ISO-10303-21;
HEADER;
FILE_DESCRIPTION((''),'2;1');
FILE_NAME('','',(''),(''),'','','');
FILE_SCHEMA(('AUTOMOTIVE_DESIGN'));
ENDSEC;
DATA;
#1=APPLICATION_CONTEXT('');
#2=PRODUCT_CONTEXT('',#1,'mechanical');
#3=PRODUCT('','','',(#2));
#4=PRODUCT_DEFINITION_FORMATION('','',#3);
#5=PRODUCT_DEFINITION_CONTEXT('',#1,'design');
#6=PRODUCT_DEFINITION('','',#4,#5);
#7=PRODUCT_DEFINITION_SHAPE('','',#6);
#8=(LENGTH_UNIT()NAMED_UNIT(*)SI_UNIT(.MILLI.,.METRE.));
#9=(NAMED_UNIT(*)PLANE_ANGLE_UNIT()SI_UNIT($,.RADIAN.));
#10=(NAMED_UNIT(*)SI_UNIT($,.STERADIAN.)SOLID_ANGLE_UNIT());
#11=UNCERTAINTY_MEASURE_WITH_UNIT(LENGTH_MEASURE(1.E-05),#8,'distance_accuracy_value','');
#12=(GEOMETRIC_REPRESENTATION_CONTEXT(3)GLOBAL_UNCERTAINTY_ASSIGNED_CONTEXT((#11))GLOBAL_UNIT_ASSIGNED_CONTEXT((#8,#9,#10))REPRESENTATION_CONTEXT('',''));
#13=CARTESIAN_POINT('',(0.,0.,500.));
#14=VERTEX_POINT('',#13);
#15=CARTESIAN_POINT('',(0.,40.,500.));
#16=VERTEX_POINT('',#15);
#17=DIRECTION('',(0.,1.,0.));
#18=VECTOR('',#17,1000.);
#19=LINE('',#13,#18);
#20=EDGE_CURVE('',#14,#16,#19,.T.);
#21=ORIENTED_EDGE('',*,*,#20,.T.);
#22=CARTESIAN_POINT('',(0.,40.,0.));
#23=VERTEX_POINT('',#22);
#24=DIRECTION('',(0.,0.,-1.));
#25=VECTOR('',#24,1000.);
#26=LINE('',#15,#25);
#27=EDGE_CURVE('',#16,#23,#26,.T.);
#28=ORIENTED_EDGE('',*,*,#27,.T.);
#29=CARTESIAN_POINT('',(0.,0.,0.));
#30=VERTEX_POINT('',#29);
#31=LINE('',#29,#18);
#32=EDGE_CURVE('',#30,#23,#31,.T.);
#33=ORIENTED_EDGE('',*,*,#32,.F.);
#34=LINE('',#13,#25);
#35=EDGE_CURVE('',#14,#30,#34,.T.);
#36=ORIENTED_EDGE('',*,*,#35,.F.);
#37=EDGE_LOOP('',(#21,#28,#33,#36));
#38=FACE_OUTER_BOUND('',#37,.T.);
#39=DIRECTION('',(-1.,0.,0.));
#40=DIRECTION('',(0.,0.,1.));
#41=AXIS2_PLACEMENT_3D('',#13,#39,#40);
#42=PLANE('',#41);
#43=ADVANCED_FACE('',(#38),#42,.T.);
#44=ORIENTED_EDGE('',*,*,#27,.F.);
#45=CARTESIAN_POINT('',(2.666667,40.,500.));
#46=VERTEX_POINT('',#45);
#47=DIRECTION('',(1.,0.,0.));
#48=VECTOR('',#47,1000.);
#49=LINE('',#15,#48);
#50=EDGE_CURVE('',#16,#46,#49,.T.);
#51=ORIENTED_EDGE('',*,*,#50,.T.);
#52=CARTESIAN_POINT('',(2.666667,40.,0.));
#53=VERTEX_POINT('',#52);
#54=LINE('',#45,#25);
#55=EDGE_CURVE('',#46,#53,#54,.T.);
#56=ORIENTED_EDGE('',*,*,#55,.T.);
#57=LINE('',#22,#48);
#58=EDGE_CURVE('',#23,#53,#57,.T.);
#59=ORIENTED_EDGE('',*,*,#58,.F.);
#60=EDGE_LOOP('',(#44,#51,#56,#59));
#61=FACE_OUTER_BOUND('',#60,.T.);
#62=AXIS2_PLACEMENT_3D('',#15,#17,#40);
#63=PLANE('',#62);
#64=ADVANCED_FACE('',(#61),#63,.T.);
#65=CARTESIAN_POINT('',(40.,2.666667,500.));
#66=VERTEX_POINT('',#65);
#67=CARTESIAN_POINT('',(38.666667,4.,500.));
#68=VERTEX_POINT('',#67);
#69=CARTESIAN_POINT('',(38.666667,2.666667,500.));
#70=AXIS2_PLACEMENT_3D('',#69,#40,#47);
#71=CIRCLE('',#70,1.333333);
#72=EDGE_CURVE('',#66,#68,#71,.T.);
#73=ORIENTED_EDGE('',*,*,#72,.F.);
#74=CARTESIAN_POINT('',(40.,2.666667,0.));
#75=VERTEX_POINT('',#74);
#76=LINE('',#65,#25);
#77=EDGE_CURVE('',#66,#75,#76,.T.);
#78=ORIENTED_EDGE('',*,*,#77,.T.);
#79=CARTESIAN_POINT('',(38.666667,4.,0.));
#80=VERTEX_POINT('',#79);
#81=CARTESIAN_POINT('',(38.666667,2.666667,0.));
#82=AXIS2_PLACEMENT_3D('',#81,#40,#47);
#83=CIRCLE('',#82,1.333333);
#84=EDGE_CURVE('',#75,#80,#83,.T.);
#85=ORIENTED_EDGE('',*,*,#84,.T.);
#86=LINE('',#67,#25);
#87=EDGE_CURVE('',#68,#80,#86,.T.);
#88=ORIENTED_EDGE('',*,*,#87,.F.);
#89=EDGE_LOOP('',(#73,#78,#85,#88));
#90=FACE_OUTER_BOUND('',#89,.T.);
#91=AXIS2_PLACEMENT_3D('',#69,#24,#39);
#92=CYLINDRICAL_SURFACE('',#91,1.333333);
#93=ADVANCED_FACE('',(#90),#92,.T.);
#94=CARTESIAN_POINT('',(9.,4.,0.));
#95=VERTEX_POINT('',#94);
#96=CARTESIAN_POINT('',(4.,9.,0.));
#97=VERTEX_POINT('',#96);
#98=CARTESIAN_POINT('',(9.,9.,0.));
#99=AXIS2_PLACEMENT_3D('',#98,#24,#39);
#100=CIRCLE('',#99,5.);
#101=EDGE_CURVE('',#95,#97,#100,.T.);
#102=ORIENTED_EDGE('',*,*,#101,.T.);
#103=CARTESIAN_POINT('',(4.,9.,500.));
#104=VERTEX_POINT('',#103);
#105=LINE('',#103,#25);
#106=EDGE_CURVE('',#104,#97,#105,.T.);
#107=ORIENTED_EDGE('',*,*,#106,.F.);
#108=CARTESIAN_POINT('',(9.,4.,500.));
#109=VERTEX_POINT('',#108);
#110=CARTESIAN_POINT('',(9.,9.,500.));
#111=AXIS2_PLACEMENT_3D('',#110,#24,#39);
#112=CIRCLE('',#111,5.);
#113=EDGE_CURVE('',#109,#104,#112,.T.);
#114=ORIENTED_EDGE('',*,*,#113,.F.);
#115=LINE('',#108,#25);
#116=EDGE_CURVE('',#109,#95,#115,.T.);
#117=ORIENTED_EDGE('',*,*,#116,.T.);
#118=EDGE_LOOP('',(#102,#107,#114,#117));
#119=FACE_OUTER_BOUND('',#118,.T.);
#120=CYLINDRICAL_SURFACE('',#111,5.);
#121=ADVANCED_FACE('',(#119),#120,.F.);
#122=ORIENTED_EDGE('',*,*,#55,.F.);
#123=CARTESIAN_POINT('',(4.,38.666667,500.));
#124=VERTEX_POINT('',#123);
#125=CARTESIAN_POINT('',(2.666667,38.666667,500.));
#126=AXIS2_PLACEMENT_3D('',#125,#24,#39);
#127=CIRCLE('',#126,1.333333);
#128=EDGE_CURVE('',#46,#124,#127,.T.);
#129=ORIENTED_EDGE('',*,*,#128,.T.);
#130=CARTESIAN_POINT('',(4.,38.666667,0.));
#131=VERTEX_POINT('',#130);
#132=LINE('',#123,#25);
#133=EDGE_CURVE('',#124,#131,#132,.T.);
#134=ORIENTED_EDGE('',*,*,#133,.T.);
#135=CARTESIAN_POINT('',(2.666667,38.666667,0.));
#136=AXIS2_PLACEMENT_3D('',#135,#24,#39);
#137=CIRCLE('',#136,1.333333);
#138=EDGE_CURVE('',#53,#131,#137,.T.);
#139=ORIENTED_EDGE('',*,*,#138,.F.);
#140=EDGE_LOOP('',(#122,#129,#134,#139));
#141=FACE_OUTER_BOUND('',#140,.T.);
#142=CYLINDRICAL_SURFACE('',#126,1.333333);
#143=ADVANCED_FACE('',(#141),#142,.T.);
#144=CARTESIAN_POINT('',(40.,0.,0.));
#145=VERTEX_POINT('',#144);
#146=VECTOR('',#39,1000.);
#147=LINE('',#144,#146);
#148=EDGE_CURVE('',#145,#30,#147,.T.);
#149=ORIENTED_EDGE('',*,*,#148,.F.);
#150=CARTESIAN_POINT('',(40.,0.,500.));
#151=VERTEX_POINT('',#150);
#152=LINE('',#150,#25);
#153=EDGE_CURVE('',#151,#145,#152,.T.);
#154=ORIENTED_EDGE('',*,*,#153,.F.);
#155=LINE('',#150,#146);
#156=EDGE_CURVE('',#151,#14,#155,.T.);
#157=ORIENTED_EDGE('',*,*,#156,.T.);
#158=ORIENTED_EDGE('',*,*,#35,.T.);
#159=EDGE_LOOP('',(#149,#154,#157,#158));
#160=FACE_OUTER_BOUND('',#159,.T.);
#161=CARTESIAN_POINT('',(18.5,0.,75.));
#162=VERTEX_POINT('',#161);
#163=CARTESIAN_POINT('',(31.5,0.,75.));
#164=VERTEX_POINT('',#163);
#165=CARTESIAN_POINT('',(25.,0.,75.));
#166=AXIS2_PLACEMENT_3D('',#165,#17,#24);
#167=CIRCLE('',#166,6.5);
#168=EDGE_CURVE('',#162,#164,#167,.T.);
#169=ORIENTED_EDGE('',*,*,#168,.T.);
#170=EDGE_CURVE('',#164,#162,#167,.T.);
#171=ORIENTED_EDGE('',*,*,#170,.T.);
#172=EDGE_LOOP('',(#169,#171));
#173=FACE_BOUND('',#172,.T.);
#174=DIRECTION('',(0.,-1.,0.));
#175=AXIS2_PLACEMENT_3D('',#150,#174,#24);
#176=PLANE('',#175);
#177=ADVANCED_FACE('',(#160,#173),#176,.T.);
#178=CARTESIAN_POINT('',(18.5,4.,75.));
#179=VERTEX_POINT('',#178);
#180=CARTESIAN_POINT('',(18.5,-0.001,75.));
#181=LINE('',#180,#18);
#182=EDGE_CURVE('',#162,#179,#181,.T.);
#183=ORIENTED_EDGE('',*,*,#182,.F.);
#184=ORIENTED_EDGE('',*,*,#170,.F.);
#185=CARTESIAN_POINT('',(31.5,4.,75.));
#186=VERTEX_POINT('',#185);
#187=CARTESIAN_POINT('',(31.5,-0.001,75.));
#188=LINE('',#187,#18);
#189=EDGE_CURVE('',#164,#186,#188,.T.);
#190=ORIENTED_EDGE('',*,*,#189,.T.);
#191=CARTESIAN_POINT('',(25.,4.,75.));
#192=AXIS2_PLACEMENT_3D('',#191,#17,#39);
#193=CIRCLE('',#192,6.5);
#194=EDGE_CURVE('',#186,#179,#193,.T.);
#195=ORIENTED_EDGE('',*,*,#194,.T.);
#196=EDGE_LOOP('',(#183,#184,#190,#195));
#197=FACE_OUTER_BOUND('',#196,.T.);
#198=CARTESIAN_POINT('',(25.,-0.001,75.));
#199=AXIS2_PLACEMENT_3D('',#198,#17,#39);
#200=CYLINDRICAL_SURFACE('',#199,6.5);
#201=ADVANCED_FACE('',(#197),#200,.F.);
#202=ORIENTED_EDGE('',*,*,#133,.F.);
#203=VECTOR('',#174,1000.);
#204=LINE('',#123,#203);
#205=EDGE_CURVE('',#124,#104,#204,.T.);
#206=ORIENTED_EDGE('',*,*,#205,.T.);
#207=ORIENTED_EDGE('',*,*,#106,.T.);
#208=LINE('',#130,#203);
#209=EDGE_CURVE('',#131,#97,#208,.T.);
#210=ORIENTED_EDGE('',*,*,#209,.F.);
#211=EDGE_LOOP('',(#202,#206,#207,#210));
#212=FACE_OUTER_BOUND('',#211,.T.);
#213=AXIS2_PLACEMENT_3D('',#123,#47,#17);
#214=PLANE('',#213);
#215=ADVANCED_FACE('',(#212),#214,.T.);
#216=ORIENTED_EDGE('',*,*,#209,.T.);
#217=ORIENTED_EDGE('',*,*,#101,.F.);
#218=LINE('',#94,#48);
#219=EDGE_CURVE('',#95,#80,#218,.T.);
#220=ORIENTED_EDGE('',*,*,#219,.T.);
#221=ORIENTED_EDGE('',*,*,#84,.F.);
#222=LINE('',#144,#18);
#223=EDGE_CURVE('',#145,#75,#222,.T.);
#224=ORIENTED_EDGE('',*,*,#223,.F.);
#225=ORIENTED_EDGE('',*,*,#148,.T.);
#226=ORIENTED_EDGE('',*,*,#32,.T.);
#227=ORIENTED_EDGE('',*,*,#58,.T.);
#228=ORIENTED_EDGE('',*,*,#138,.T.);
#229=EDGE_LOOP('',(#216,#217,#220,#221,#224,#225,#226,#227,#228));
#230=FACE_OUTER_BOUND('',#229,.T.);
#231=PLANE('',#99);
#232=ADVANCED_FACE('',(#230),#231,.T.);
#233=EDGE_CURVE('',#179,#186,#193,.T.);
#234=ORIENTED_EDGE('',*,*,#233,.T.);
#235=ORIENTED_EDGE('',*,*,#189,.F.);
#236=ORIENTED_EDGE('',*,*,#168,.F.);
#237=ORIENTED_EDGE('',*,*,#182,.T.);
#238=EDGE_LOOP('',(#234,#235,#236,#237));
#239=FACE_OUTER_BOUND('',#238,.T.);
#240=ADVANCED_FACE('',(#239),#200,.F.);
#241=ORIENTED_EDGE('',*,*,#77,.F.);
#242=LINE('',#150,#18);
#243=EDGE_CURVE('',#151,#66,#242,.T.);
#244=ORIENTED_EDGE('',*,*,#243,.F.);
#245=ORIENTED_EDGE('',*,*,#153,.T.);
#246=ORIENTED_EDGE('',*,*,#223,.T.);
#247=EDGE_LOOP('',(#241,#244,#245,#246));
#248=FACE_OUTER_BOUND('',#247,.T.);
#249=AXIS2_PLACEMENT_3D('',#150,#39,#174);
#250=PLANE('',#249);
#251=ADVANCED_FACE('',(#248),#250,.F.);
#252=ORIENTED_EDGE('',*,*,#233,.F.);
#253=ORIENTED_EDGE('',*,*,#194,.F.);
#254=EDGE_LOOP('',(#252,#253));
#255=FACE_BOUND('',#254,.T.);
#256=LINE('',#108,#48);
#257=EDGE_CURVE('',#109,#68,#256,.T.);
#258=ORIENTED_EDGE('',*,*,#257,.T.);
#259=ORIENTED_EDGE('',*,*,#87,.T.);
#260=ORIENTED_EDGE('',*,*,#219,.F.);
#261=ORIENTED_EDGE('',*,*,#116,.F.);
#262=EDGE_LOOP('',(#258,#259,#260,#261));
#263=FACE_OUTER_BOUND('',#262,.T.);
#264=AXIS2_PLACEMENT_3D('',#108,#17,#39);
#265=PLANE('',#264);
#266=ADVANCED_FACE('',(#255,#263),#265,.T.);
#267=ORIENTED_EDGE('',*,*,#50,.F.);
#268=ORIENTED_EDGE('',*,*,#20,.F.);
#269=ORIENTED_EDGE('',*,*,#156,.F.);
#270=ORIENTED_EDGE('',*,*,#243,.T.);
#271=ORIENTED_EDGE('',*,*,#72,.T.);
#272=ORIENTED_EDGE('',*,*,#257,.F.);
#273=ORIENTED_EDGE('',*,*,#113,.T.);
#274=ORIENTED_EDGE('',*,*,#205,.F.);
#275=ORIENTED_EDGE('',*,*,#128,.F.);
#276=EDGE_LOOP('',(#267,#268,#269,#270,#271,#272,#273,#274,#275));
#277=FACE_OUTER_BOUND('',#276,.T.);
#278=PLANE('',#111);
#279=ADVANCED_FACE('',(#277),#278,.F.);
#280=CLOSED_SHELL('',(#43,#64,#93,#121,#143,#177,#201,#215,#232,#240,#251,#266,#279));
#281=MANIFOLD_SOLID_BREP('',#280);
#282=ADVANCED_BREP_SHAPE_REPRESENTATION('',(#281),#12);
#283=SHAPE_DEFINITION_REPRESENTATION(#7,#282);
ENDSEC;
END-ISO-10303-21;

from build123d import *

# Parameters (mm, degrees)
BOSS_EXTRUDE1_DEPTH = 500
CUT_EXTRUDE1_REACH  = 504.888
SKETCH_1_R          = 6.5


with BuildPart() as part:
    # Sketch1 → Boss-Extrude1 (new body)
    with BuildSketch(Plane.XY):
        with BuildLine():
            Line((0, 0), (0, 40))
            Line((0, 40), (2.666666667, 40))
            ThreePointArc((2.666666667, 40), (3.609475708, 39.609475708), (4, 38.666666667))
            Line((4, 38.666666667), (4, 9))
            ThreePointArc((4, 9), (5.464466094, 5.464466094), (9, 4))
            Line((9, 4), (38.666666667, 4))
            ThreePointArc((38.666666667, 4), (39.609475708, 3.609475708), (40, 2.666666667))
            Line((40, 2.666666667), (40, 0))
            Line((40, 0), (0, 0))
        make_face()
    extrude(amount=BOSS_EXTRUDE1_DEPTH)

    # 草图1 → Cut-Extrude1 (cut, up to next)
    with BuildSketch(Plane(origin=(0, 4, 0), x_dir=(1, 0, 0), z_dir=(0, 1, 0)), mode=Mode.PRIVATE) as cut_extrude1_sk1:
        with Locations(Location((25, -75, 0), (0, 0, 180))):
            Circle(SKETCH_1_R)
    cut_extrude1_tool1 = extrude(cut_extrude1_sk1.sketch, amount=-CUT_EXTRUDE1_REACH, mode=Mode.PRIVATE) & part.part
    add(cut_extrude1_tool1.solids().sort_by_distance((25, 4, 75))[0], mode=Mode.SUBTRACT)


solid = part.part
